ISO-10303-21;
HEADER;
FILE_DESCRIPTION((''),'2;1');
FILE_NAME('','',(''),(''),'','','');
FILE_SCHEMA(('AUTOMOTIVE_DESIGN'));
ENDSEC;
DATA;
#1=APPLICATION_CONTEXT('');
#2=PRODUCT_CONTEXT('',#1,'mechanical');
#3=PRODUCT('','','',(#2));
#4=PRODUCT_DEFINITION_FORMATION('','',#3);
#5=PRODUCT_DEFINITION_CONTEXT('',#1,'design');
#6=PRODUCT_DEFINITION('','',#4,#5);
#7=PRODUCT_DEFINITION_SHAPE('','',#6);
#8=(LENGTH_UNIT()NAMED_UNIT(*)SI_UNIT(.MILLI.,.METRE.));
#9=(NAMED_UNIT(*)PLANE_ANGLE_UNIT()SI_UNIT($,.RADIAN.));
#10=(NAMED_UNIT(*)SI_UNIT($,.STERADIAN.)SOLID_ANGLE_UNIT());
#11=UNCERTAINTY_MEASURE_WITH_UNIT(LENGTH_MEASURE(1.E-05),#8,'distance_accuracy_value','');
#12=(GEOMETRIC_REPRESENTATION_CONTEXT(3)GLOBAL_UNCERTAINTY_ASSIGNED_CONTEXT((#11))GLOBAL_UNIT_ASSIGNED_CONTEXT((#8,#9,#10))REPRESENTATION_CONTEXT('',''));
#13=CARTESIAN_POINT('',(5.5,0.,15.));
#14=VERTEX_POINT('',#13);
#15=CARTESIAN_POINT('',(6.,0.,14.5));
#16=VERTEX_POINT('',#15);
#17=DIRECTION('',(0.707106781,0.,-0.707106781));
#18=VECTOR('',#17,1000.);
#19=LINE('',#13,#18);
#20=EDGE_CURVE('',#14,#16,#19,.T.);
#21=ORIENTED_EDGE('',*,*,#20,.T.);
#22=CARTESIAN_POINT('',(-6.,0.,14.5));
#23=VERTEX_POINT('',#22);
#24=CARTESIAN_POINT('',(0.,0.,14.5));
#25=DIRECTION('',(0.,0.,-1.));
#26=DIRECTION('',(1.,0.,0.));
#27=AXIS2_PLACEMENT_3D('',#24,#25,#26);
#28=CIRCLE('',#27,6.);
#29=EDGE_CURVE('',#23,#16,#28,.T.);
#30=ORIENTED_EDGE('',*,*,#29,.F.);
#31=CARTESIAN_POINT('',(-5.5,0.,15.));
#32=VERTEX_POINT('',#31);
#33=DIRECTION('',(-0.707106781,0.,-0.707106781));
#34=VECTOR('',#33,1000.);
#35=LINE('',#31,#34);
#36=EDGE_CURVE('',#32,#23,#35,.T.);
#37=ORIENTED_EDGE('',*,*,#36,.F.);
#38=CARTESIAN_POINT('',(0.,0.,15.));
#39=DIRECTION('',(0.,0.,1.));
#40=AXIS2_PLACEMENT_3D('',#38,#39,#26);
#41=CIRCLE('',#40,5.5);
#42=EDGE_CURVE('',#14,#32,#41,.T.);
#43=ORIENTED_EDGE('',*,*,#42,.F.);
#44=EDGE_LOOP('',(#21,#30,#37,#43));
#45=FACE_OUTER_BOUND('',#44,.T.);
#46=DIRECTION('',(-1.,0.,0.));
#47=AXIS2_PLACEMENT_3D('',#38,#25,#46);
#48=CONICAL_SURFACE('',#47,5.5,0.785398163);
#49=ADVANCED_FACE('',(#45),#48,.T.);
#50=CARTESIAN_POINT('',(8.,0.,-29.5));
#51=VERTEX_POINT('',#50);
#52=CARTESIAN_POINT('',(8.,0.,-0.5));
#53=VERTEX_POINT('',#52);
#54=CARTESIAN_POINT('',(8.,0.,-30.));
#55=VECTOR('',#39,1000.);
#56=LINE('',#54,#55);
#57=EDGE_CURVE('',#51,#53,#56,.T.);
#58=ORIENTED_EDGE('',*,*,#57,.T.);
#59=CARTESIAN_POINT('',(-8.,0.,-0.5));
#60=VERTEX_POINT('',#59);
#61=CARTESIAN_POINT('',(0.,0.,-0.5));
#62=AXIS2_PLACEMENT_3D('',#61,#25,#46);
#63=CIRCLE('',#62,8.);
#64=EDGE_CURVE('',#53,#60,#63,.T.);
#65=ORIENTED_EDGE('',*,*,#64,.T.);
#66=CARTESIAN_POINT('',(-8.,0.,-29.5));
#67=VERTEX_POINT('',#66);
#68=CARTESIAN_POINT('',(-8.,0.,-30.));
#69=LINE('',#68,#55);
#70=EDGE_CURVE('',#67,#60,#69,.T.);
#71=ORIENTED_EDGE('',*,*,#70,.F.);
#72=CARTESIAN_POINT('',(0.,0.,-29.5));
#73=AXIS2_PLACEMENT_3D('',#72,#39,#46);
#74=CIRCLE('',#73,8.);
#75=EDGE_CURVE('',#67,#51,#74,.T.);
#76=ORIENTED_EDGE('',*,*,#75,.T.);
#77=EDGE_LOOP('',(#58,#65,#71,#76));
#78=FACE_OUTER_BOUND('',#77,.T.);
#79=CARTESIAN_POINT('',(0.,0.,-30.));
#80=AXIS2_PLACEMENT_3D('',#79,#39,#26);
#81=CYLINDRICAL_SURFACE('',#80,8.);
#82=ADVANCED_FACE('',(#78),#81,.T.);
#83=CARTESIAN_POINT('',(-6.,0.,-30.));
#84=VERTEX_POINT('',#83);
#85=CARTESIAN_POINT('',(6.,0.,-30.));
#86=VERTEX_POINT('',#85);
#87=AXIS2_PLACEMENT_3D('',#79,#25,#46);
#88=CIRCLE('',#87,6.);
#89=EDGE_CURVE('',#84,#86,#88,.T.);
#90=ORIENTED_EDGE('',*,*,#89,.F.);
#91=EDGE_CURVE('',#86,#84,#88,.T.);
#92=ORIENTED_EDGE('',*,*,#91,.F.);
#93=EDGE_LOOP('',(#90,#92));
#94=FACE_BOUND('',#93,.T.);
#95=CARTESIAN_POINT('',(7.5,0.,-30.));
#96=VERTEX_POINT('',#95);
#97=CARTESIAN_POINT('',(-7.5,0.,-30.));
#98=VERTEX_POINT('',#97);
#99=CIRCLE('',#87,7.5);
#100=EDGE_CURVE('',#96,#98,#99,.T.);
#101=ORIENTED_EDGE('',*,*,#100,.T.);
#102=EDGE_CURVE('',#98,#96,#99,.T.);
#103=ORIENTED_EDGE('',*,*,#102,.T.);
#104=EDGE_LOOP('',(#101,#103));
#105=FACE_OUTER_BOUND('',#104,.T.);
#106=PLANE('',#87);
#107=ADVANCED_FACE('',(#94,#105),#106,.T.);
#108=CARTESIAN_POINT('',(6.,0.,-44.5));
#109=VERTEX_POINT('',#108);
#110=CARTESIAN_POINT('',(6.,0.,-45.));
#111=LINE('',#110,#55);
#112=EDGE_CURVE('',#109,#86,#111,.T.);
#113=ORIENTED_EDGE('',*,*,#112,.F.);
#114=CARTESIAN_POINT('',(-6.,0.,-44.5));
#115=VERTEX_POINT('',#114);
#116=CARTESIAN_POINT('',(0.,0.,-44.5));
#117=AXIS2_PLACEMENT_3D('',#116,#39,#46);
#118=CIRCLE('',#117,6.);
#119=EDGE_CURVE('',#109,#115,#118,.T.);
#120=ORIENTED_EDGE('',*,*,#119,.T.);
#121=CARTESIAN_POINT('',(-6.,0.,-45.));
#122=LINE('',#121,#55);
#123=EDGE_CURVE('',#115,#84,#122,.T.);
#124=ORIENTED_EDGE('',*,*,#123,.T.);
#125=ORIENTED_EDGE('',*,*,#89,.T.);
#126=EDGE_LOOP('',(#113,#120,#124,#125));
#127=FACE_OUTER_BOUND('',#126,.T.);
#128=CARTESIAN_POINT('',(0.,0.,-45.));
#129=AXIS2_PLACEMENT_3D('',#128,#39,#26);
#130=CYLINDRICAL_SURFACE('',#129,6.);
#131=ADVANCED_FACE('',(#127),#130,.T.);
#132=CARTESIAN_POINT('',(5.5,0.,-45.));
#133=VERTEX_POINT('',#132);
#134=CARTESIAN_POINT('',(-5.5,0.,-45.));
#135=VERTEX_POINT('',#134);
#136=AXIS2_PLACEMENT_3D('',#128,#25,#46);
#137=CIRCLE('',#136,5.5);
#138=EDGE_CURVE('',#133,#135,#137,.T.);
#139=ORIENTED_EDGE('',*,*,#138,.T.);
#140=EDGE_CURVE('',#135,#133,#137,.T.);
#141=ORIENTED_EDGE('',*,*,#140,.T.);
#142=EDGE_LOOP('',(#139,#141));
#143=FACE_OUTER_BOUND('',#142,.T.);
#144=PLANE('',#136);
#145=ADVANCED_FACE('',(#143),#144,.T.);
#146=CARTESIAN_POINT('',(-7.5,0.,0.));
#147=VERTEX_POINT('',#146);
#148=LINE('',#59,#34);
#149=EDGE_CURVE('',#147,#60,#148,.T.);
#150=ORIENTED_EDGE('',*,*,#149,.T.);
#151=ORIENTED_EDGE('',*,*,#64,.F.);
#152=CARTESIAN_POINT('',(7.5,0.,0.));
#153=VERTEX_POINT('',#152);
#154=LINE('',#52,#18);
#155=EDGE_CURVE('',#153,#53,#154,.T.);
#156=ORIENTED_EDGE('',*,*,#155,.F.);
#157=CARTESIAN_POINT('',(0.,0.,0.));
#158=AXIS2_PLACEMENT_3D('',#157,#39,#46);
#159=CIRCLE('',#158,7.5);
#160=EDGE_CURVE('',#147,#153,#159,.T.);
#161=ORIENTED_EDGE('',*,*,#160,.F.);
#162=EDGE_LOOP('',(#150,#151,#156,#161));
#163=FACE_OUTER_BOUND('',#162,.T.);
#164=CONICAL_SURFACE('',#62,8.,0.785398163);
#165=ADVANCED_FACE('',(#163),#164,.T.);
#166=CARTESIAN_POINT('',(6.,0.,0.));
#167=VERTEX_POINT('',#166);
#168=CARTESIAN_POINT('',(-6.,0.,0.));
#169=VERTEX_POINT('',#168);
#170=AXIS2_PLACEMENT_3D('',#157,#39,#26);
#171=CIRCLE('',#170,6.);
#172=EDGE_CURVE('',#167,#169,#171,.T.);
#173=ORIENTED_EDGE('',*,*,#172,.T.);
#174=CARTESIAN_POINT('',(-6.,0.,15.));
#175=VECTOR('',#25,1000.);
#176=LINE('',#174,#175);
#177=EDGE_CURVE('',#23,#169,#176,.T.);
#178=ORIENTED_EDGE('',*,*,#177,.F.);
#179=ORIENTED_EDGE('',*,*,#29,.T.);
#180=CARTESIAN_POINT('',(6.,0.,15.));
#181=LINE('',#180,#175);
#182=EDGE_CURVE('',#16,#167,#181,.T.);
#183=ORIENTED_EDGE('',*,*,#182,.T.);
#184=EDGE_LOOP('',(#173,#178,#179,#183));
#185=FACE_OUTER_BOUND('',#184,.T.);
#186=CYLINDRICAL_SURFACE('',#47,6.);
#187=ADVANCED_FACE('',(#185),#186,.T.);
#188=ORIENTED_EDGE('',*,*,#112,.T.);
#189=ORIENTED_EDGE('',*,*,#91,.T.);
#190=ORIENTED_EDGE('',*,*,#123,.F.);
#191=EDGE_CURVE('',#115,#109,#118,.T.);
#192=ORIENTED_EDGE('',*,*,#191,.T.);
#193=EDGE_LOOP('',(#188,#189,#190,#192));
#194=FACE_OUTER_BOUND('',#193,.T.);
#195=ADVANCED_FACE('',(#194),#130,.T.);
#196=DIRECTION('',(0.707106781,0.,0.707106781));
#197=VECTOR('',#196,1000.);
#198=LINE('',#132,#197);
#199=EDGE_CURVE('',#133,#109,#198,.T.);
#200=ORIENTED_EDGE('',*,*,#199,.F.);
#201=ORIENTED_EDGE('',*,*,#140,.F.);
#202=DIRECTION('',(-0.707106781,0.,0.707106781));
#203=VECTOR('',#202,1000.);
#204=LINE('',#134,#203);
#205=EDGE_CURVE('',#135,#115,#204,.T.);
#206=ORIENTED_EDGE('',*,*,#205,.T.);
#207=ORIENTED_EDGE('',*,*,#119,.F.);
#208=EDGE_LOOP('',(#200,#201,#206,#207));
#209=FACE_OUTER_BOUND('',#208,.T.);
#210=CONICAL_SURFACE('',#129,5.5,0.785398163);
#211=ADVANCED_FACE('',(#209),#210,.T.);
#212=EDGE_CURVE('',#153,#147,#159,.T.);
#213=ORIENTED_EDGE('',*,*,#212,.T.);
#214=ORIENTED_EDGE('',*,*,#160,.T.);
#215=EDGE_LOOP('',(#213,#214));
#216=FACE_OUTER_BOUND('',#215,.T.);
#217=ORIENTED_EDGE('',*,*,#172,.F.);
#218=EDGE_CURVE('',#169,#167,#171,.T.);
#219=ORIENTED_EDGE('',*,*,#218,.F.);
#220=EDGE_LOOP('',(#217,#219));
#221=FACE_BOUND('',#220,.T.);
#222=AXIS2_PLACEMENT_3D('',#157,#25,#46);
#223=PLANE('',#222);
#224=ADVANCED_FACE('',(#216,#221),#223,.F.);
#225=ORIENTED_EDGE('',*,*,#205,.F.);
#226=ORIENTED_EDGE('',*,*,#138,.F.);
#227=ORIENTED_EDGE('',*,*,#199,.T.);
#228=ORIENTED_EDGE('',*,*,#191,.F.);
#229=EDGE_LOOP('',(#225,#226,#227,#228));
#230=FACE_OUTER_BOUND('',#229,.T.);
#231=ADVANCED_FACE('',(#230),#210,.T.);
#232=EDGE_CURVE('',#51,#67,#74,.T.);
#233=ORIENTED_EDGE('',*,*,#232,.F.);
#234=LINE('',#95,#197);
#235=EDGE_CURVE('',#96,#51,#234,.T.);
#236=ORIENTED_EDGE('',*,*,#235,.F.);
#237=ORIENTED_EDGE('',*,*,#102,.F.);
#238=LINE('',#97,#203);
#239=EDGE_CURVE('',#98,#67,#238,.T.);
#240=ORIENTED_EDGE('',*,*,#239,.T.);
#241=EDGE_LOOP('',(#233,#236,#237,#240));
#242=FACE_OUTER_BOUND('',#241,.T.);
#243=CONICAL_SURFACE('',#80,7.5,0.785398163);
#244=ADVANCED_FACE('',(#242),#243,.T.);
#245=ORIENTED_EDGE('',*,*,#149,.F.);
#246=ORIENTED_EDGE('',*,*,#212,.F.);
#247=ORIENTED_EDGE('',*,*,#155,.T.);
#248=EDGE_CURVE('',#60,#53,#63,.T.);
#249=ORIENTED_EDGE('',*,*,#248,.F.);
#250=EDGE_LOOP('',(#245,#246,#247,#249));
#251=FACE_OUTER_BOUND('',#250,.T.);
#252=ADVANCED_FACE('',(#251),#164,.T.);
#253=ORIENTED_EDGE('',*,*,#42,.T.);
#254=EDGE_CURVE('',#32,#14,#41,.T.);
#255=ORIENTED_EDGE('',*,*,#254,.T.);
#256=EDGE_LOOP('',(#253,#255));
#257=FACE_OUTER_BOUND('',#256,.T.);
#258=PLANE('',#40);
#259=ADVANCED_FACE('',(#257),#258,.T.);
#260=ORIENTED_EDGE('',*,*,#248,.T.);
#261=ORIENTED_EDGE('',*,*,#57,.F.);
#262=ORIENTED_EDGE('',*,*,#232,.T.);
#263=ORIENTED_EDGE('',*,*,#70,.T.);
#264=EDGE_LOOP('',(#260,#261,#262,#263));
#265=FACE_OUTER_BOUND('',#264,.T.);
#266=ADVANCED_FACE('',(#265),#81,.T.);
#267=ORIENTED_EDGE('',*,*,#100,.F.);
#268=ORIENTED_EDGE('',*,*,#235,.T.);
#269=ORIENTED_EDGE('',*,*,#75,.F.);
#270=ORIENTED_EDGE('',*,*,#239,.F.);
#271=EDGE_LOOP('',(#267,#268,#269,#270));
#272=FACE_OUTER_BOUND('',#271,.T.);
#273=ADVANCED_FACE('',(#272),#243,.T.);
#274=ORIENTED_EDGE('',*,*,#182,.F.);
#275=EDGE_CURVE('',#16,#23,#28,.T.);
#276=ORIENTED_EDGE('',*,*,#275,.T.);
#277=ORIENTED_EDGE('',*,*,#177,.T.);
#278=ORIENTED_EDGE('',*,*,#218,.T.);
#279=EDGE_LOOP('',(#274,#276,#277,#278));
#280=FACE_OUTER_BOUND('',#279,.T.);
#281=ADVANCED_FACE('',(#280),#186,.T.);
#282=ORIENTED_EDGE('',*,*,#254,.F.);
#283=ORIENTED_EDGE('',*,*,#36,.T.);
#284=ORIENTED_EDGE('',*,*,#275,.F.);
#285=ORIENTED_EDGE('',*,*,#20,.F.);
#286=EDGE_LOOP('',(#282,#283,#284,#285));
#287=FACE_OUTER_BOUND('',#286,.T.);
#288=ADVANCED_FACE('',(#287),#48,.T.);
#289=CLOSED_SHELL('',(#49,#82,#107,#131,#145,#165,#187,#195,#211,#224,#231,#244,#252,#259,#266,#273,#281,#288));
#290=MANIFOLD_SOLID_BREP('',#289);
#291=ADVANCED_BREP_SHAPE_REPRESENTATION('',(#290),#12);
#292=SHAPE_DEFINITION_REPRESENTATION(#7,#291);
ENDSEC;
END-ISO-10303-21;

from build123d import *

# Parameters (mm, degrees)
SKETCH1_R           = 6
BOSS_EXTRUDE1_DEPTH = 15
SKETCH2_R           = 8
BOSS_EXTRUDE2_DEPTH = 30
BOSS_EXTRUDE3_START = 15
SKETCH3_R           = 6
BOSS_EXTRUDE3_DEPTH = 15
CHAMFER1_SIZE       = 0.5


with BuildPart() as part:
    # Sketch1 → Boss-Extrude1 (new body)
    with BuildSketch(Plane.XY):
        Circle(SKETCH1_R)
    extrude(amount=BOSS_EXTRUDE1_DEPTH)

    # Sketch2 → Boss-Extrude2 (add)
    with BuildSketch(Plane(origin=(0, 0, 0), x_dir=(-1, 0, 0), z_dir=(0, 0, -1))):
        Circle(SKETCH2_R)
    extrude(amount=BOSS_EXTRUDE2_DEPTH)

    # Sketch3 → Boss-Extrude3 (add)
    with BuildSketch(Plane(origin=(0, 0, -30), x_dir=(-1, 0, 0), z_dir=(0, 0, -1)).offset(BOSS_EXTRUDE3_START)):
        with Locations(Location((0, 0, 0), (0, 0, 180))):
            Circle(SKETCH3_R)
    extrude(amount=-BOSS_EXTRUDE3_DEPTH)

    # Chamfer1
    chamfer1_edges = [part.edges().sort_by_distance(p)[0] for p in [
        (-6, 0, -45),
        (-6, 0, 15),
        (8, 0, 0),
        (8, 0, -30),
    ]]
    chamfer(chamfer1_edges, length=CHAMFER1_SIZE)


solid = part.part
